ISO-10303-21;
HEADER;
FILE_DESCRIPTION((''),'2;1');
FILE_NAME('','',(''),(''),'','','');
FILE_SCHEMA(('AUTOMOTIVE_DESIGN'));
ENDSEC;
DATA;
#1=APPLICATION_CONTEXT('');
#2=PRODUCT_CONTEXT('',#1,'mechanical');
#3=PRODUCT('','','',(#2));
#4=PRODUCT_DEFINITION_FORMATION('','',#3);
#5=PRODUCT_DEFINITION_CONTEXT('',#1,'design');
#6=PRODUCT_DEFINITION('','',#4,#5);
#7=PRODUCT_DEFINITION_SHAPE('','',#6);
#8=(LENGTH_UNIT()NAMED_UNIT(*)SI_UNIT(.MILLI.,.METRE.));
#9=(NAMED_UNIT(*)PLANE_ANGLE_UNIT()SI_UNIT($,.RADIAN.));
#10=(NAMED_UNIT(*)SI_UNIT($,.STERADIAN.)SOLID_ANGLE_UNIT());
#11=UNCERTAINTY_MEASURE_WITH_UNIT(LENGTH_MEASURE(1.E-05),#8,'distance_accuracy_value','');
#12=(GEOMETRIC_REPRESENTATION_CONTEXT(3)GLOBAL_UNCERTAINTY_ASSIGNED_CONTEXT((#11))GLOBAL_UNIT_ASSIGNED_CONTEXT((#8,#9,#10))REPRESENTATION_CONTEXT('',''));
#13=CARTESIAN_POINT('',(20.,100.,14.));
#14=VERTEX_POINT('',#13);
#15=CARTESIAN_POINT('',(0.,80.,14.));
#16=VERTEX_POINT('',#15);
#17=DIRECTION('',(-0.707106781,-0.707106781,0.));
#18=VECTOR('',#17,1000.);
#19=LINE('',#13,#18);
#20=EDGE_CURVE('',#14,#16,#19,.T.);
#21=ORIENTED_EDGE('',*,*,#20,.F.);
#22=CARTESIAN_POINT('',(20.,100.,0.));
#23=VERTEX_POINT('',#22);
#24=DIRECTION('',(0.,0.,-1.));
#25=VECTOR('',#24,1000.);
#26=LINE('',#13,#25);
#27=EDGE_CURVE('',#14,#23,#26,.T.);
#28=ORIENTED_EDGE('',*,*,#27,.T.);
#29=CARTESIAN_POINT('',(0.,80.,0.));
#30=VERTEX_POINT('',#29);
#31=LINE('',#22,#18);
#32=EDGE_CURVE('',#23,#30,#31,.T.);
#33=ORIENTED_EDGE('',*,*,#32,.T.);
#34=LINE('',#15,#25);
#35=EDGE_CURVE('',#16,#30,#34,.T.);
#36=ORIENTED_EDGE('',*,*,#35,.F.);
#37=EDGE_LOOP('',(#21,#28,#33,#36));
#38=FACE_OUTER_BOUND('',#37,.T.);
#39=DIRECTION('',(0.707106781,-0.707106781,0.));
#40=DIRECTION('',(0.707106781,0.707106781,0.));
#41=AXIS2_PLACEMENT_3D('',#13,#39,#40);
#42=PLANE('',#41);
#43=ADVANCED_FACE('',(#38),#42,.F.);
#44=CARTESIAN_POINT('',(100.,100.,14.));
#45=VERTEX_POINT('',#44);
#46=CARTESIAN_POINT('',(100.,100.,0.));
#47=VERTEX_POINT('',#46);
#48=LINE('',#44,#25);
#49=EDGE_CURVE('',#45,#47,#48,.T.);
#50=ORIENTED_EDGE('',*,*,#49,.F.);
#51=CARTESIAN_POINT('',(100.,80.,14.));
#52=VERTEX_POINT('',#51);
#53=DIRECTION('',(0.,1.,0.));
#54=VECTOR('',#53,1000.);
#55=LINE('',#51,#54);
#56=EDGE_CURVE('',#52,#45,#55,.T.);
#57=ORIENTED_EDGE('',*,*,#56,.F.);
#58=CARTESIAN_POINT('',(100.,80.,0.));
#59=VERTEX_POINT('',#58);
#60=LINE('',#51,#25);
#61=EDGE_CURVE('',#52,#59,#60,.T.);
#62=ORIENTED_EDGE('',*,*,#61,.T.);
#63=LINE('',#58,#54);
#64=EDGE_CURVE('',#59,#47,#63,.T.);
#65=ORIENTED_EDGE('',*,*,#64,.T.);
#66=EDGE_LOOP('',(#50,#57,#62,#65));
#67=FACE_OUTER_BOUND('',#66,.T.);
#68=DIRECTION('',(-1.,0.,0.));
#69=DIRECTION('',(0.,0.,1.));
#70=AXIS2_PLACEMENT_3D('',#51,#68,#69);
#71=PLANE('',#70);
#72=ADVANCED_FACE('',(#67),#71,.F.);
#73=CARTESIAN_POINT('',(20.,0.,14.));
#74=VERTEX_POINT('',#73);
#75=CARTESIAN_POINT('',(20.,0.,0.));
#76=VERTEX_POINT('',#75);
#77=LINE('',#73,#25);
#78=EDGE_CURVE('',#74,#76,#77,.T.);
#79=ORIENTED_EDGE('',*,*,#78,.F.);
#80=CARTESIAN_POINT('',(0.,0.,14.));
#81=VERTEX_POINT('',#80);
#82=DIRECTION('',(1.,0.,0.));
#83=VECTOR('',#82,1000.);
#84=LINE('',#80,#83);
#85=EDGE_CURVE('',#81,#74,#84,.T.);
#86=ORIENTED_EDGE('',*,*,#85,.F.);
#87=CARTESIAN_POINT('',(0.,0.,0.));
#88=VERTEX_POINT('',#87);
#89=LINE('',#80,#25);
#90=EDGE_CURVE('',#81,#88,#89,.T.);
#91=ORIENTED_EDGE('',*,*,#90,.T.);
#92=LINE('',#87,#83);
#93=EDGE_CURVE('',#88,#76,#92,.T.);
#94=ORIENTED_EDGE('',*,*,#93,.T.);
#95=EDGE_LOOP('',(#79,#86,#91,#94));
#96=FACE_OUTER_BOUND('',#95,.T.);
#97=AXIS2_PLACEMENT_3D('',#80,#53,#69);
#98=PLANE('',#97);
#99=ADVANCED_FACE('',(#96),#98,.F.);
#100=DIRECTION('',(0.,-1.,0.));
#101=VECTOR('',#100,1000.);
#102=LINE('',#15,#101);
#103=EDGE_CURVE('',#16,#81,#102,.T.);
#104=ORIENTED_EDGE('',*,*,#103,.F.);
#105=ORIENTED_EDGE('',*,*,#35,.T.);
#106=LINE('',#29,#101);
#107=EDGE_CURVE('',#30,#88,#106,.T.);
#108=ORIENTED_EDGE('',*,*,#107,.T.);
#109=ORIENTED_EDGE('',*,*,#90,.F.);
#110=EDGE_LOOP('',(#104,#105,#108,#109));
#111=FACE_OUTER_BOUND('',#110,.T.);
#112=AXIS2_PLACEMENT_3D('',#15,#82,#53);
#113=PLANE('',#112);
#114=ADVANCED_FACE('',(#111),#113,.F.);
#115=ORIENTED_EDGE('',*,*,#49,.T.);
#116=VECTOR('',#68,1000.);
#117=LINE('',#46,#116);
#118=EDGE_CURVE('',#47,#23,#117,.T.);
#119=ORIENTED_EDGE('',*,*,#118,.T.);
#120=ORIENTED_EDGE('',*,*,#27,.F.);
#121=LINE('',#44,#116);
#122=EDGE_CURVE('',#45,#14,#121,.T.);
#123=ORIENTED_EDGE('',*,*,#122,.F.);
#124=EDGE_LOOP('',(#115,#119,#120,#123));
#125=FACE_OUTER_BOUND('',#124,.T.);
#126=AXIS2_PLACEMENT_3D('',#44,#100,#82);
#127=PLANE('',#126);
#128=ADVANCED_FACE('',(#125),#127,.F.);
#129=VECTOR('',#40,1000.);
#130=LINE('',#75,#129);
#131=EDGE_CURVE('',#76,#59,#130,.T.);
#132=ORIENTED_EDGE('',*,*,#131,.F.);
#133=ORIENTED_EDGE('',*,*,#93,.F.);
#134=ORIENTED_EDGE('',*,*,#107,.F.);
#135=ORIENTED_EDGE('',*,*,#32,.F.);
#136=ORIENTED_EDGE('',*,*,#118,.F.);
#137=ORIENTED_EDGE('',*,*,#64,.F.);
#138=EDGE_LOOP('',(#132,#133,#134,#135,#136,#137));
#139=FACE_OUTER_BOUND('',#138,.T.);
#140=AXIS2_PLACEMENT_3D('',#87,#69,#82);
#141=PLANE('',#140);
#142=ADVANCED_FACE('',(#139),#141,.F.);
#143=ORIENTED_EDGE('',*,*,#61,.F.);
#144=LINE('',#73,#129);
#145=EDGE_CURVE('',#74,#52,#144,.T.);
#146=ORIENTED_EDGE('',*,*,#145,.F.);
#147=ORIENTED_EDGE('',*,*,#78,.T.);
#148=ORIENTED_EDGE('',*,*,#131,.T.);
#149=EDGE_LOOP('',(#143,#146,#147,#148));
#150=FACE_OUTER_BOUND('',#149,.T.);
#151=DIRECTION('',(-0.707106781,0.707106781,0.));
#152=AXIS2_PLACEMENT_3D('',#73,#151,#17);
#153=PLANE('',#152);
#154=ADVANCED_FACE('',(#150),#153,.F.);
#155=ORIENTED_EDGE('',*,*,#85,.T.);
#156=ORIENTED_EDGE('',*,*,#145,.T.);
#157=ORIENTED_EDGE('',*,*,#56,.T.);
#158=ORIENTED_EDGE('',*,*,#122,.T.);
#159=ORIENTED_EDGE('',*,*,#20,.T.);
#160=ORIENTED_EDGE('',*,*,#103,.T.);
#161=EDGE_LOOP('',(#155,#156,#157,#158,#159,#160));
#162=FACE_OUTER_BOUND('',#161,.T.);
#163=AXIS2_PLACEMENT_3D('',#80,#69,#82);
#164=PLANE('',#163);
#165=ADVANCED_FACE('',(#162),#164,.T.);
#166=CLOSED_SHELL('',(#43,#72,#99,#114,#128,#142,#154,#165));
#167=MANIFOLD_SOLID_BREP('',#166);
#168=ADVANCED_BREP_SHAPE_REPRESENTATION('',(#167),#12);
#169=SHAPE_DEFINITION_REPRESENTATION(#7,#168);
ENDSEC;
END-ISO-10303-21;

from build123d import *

# Parameters (mm, degrees)
EXTRUDE_1_DEPTH = 14


with BuildPart() as part:
    # 草图1 → 凸台-拉伸1 (new body)
    with BuildSketch(Plane.XY):
        Polygon((0, 0), (20, 0), (100, 80), (100, 100), (20, 100), (0, 80), align=None)
    extrude(amount=EXTRUDE_1_DEPTH)


solid = part.part
